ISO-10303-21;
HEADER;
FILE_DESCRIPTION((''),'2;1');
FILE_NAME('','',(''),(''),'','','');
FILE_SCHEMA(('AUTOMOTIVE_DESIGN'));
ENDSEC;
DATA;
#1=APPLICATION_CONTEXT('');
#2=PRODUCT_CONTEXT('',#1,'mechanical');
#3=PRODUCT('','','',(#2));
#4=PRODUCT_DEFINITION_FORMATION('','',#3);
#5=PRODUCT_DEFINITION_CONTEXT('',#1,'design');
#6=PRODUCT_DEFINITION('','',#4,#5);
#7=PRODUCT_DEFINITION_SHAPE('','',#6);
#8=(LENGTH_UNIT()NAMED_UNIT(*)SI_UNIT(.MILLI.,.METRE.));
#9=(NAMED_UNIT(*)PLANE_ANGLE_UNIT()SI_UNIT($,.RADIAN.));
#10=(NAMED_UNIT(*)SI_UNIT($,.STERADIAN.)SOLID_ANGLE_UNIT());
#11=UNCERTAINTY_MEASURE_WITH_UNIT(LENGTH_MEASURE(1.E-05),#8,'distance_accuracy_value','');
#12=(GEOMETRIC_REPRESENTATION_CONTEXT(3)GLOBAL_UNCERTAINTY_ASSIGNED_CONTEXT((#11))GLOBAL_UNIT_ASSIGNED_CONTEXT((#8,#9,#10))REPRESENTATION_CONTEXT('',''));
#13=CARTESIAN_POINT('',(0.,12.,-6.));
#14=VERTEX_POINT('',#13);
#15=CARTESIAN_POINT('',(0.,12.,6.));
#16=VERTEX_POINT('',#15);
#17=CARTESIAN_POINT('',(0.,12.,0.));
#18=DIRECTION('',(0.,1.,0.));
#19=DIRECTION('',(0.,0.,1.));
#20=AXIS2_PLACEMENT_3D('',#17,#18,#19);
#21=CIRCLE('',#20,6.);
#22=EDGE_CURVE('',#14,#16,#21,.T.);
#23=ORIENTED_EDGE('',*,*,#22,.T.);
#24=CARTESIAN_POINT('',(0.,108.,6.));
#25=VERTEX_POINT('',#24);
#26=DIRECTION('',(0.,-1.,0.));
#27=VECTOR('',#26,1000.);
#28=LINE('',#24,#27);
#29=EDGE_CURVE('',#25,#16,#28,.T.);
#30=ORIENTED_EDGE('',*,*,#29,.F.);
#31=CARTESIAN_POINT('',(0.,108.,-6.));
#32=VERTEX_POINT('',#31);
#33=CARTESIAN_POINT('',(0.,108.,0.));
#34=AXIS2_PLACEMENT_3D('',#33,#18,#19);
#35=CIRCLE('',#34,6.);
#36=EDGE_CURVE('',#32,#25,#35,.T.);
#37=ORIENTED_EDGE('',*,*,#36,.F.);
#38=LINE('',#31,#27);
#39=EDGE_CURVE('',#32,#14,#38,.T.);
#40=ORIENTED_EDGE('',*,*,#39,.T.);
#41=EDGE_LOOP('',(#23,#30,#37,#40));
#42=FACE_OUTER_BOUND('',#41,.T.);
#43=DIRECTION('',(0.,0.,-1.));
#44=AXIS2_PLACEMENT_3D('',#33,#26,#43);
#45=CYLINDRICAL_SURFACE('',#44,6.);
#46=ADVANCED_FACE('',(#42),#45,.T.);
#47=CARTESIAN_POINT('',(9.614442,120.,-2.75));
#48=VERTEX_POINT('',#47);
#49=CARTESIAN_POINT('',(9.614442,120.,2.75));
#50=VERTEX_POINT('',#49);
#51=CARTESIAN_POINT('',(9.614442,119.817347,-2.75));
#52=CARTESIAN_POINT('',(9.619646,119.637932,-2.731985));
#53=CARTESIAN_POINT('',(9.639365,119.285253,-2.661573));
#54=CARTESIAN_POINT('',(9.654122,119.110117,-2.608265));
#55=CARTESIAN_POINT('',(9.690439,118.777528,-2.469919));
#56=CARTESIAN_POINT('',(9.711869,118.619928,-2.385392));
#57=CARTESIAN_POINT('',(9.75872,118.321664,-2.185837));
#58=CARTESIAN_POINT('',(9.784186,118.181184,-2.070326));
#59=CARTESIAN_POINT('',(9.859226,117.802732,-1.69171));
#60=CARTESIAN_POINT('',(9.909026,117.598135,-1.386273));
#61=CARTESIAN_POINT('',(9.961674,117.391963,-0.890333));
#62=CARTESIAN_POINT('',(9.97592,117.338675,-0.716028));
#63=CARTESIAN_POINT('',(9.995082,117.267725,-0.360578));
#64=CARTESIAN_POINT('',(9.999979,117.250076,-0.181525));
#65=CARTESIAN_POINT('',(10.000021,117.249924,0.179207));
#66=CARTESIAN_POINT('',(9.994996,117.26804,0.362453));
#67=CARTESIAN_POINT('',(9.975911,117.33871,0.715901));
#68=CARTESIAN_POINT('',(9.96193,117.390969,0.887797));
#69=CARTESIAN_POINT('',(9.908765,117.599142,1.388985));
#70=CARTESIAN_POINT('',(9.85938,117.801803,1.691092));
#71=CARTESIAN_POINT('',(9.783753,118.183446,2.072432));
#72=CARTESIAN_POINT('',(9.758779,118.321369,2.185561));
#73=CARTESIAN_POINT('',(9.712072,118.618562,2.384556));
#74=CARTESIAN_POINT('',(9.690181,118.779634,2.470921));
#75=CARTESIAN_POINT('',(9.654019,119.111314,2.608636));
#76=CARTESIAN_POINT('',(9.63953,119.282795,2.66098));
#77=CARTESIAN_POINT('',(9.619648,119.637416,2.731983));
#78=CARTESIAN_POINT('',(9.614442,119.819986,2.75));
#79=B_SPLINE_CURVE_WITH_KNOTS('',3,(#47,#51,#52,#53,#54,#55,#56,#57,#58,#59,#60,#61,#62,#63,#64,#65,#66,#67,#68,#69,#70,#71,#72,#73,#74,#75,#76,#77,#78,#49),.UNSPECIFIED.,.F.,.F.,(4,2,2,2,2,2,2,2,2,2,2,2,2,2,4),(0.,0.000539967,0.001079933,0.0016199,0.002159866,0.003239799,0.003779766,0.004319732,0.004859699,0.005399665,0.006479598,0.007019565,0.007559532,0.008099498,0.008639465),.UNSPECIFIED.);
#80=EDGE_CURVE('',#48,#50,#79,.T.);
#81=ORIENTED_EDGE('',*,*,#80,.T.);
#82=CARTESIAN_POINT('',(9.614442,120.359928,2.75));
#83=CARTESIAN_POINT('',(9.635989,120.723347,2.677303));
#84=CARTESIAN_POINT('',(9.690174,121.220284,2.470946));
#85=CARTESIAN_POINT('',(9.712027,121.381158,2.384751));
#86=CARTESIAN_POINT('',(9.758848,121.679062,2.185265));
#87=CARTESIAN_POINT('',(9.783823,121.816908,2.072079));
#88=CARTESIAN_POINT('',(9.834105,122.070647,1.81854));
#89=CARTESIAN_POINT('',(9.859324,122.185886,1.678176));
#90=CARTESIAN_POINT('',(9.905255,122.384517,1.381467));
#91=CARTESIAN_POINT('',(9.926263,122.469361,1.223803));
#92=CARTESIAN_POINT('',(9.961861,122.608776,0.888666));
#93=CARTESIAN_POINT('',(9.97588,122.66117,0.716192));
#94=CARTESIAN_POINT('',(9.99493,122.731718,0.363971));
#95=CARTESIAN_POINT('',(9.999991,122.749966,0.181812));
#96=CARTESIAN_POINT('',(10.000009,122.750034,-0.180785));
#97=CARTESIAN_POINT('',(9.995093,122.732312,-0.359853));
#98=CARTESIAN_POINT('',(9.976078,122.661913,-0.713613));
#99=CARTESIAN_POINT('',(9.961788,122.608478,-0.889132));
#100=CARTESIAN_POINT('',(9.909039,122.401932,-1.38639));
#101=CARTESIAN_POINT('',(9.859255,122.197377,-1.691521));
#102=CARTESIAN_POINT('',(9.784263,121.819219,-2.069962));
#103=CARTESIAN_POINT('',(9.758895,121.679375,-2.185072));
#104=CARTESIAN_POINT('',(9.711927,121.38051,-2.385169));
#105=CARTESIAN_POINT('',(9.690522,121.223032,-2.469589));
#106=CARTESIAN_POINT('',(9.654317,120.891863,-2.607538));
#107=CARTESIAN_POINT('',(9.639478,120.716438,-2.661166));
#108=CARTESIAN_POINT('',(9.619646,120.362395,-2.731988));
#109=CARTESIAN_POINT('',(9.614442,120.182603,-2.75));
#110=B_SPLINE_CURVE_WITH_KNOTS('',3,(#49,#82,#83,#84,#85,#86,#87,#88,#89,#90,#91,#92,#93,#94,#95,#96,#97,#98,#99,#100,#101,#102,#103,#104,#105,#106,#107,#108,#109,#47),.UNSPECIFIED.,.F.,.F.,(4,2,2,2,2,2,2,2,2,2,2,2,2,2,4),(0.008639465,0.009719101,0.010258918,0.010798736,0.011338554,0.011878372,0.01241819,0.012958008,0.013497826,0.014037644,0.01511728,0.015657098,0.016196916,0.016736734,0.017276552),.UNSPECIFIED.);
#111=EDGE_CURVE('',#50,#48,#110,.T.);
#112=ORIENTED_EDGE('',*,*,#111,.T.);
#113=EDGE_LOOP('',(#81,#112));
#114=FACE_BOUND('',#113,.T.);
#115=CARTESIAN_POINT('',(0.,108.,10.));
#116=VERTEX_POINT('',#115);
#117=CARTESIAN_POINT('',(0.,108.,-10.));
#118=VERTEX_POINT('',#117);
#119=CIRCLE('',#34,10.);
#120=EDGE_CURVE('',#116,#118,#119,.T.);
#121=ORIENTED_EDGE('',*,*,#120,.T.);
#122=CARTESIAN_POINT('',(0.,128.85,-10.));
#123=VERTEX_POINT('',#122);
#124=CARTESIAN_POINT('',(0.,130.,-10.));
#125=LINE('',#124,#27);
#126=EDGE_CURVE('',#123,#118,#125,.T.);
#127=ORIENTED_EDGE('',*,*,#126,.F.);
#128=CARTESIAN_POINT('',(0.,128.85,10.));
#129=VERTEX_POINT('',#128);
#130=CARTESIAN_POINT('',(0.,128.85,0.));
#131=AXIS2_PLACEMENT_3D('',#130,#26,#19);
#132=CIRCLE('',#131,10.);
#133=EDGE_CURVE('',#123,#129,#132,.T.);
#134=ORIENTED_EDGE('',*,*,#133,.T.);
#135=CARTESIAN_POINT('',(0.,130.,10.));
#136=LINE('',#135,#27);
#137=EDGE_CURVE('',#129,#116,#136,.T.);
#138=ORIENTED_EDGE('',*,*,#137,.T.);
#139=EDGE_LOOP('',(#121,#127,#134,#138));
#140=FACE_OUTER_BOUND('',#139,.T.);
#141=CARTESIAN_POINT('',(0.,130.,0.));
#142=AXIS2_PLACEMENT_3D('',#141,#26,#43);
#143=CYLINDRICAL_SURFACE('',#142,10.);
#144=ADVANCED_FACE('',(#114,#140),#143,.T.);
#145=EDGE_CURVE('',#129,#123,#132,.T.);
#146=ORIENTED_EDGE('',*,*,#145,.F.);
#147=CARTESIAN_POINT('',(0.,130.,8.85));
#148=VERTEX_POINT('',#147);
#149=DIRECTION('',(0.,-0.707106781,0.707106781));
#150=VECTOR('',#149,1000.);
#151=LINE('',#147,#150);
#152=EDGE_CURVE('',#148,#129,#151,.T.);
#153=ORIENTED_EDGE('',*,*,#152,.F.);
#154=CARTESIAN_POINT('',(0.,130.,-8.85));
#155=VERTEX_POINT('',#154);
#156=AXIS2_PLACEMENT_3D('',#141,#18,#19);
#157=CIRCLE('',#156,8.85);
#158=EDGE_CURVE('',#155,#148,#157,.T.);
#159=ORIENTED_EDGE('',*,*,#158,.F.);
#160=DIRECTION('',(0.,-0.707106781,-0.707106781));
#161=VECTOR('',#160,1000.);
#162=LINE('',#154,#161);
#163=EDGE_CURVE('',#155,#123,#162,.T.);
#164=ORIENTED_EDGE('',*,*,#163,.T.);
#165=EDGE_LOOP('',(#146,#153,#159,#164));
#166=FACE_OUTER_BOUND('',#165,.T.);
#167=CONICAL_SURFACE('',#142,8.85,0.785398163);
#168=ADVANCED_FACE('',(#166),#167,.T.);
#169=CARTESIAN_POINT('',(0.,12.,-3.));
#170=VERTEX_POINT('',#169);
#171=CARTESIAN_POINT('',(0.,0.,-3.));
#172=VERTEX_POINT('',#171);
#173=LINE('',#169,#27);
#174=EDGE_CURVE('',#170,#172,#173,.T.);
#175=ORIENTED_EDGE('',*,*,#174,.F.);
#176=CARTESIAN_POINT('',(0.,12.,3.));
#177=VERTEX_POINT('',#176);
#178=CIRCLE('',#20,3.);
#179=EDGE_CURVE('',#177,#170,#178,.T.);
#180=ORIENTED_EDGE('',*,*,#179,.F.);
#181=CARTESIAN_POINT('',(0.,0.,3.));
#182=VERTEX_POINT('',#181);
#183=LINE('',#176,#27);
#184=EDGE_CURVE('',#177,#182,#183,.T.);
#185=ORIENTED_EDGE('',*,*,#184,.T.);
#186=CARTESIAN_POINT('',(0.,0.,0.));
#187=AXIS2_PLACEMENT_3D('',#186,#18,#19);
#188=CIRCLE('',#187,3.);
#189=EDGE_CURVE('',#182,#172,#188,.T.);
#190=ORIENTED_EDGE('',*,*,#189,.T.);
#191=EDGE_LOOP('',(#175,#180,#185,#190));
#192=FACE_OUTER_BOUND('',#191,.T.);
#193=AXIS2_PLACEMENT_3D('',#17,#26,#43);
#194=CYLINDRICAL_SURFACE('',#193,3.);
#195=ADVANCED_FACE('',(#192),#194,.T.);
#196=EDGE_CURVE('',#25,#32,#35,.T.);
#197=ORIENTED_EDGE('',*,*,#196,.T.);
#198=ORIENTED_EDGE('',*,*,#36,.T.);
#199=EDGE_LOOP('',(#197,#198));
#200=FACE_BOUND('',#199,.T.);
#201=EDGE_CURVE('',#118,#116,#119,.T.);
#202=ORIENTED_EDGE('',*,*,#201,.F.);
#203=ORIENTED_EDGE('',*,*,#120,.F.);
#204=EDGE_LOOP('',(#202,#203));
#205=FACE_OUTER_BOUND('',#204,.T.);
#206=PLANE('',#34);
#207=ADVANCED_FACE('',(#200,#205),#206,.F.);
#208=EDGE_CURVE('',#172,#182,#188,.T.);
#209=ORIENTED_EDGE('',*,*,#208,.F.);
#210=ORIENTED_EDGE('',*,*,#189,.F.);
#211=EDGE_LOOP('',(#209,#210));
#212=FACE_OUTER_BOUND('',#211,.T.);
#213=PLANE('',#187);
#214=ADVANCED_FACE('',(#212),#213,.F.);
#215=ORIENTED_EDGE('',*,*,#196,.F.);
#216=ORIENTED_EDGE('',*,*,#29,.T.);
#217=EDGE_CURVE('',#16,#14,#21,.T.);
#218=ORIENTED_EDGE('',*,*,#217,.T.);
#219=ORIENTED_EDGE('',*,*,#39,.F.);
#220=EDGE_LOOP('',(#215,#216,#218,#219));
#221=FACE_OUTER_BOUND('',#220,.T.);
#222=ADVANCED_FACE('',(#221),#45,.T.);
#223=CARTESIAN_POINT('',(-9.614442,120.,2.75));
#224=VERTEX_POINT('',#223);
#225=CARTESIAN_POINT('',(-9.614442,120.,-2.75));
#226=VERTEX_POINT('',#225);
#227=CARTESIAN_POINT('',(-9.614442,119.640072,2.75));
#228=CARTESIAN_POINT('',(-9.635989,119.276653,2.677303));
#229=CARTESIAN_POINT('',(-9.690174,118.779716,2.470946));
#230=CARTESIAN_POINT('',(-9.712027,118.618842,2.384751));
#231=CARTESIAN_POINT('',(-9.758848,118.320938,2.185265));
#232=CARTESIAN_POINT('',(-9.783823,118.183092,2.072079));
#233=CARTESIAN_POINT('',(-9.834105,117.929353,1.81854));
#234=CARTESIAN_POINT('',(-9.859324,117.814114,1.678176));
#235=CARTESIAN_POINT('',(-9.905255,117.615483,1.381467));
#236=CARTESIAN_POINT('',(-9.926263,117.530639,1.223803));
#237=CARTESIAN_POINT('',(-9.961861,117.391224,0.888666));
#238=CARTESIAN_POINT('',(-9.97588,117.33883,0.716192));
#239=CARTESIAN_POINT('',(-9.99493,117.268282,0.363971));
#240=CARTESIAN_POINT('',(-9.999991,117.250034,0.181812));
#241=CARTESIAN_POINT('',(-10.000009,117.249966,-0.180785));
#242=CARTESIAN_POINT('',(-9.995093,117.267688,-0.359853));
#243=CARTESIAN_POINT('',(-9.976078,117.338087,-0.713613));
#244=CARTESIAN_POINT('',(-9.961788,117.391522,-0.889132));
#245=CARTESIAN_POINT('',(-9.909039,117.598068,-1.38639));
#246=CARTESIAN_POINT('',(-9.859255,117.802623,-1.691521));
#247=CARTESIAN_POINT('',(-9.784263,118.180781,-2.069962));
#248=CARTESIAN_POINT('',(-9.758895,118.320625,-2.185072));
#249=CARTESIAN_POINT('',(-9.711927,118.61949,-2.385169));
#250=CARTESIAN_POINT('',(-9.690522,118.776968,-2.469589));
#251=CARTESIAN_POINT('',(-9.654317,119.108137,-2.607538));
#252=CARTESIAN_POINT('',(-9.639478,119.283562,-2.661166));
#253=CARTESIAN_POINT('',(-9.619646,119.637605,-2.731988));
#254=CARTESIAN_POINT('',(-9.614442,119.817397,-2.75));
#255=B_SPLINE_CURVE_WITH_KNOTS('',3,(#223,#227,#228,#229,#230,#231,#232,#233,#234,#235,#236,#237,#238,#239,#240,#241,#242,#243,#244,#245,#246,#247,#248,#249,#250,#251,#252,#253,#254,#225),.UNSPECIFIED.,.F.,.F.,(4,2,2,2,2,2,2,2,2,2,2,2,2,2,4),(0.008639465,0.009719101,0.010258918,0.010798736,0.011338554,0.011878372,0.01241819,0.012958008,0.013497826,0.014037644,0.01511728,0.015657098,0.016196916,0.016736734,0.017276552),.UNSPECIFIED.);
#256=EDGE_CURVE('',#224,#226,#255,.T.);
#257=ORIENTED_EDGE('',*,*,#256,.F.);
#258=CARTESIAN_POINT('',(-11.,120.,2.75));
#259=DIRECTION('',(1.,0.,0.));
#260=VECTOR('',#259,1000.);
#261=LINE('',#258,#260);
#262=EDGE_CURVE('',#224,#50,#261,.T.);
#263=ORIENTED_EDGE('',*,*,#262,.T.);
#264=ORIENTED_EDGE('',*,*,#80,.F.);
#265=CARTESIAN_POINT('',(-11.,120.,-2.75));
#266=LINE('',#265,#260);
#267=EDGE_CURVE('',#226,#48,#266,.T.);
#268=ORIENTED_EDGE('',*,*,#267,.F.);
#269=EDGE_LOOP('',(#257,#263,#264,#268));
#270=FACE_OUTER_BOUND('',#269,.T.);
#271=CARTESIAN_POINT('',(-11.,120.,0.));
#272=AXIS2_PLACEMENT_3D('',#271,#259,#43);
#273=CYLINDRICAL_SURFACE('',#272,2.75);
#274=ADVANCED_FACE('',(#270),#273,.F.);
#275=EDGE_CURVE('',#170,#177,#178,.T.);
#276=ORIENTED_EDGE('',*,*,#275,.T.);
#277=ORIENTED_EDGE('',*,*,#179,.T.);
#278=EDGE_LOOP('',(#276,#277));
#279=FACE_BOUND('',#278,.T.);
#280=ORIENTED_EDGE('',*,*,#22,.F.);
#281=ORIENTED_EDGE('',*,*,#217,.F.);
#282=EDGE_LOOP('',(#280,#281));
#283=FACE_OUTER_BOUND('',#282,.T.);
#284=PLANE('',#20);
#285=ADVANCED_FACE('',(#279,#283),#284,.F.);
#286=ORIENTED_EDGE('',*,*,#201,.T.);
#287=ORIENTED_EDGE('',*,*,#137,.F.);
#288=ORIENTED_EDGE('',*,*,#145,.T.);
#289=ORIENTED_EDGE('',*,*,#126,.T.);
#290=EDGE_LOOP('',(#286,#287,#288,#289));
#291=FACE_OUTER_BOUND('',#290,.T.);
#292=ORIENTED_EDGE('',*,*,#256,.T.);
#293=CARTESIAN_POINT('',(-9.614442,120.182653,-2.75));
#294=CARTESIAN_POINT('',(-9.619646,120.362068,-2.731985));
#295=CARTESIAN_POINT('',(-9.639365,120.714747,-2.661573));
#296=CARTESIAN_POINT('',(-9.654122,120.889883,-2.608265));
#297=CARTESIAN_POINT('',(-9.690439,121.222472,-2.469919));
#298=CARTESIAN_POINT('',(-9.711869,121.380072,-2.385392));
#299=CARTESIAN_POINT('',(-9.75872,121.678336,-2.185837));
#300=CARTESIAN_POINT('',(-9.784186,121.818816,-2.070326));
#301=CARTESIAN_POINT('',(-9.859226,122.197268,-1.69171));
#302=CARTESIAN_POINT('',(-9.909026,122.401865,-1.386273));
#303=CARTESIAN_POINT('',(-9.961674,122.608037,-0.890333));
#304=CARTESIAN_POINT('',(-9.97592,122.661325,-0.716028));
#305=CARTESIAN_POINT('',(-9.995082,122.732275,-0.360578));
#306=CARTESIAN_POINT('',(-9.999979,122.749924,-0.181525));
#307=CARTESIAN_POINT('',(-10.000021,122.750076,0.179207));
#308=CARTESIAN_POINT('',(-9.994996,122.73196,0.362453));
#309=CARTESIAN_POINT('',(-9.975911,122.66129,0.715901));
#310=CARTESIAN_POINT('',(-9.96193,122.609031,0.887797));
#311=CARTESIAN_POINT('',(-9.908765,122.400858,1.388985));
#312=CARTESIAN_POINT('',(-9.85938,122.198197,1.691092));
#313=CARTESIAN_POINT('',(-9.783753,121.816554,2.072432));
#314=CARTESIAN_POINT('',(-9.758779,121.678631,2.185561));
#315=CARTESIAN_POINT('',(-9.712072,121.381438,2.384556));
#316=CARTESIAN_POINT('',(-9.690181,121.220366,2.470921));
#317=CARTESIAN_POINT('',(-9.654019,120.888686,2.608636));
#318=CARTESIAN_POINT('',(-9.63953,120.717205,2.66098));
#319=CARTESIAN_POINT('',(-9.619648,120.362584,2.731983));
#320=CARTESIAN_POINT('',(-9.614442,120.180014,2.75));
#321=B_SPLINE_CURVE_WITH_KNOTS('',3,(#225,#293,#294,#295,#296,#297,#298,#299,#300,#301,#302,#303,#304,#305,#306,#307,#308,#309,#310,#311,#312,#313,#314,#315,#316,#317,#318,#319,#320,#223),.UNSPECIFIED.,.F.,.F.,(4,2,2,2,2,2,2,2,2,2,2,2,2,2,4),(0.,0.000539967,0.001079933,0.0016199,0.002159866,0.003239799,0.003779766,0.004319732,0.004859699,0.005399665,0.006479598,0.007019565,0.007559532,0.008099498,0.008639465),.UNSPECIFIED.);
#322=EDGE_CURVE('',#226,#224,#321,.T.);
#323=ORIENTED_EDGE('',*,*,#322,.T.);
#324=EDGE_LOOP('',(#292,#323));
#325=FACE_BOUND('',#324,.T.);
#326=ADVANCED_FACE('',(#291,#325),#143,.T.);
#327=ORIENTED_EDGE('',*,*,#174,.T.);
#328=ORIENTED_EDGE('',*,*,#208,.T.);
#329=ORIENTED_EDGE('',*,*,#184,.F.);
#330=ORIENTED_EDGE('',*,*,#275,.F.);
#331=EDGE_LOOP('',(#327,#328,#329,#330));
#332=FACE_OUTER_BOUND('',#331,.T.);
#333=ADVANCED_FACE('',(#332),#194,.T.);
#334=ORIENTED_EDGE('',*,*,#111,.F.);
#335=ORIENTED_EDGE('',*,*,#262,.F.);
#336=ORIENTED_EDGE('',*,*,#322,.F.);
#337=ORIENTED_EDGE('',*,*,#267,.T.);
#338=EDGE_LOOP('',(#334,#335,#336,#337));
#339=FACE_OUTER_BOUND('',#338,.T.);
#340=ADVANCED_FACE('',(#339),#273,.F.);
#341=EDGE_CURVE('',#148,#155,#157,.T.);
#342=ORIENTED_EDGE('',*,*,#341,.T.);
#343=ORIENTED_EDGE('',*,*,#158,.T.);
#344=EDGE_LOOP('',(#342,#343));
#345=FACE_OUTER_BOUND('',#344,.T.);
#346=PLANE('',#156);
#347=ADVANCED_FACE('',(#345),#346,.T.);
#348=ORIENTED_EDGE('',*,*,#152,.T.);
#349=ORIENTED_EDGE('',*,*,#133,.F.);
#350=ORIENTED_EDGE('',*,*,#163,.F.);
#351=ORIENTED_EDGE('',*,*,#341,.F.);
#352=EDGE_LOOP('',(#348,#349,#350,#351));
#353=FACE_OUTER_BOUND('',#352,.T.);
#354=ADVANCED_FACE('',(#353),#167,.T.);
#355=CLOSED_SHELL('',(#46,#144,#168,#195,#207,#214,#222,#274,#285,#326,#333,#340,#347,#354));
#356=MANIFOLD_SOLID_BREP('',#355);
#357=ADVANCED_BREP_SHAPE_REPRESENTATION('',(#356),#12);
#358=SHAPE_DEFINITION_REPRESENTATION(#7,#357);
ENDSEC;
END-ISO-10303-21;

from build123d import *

# Parameters (mm, degrees)
TIP_PIN_SKETCH_6_R        = 3
TIP_PIN_6X12_DEPTH        = 12
SHAFT_SKETCH_12_R         = 6
SHAFT_12X96_DEPTH         = 96
HEAD_SKETCH_20_R          = 10
HEAD_20X22_DEPTH          = 22
CROSS_HOLE_SKETCH_5_5_R   = 2.75
CROSS_HOLE_5_5_DEPTH      = 11
HEAD_CHAMFER_1_15X45_SIZE = 1.15


with BuildPart() as part:
    # Tip Pin Sketch Ø6 → Tip Pin Ø6x12 (new body)
    with BuildSketch(Plane(origin=(0, 0, 0), x_dir=(1, 0, 0), z_dir=(0, 1, 0))):
        with Locations(Location((0, 0, 0), (0, 0, 270))):
            Circle(TIP_PIN_SKETCH_6_R)
    extrude(amount=TIP_PIN_6X12_DEPTH)

    # Shaft Sketch Ø12 → Shaft Ø12x96 (add)
    with BuildSketch(Plane(origin=(0, 12, 0), x_dir=(1, 0, 0), z_dir=(0, 1, 0))):
        with Locations(Location((0, 0, 0), (0, 0, 270))):
            Circle(SHAFT_SKETCH_12_R)
    extrude(amount=SHAFT_12X96_DEPTH)

    # Head Sketch Ø20 → Head Ø20x22 (add)
    with BuildSketch(Plane(origin=(0, 108, 0), x_dir=(1, 0, 0), z_dir=(0, 1, 0))):
        with Locations(Location((0, 0, 0), (0, 0, 270))):
            Circle(HEAD_SKETCH_20_R)
    extrude(amount=HEAD_20X22_DEPTH)

    # Cross Hole Sketch Ø5.5 → Cross Hole Ø5.5 (cut, symmetric)
    with BuildSketch(Plane(origin=(0, 0, 0), x_dir=(0, 0, -1), z_dir=(1, 0, 0))):
        with Locations((0, 120)):
            Circle(CROSS_HOLE_SKETCH_5_5_R)
    extrude(amount=CROSS_HOLE_5_5_DEPTH, both=True, mode=Mode.SUBTRACT)

    # Head Chamfer 1.15x45°
    head_chamfer_1_15x45_edges = [part.edges().sort_by_distance(p)[0] for p in [
        (0, 130, -10),
    ]]
    chamfer(head_chamfer_1_15x45_edges, length=HEAD_CHAMFER_1_15X45_SIZE)


solid = part.part
